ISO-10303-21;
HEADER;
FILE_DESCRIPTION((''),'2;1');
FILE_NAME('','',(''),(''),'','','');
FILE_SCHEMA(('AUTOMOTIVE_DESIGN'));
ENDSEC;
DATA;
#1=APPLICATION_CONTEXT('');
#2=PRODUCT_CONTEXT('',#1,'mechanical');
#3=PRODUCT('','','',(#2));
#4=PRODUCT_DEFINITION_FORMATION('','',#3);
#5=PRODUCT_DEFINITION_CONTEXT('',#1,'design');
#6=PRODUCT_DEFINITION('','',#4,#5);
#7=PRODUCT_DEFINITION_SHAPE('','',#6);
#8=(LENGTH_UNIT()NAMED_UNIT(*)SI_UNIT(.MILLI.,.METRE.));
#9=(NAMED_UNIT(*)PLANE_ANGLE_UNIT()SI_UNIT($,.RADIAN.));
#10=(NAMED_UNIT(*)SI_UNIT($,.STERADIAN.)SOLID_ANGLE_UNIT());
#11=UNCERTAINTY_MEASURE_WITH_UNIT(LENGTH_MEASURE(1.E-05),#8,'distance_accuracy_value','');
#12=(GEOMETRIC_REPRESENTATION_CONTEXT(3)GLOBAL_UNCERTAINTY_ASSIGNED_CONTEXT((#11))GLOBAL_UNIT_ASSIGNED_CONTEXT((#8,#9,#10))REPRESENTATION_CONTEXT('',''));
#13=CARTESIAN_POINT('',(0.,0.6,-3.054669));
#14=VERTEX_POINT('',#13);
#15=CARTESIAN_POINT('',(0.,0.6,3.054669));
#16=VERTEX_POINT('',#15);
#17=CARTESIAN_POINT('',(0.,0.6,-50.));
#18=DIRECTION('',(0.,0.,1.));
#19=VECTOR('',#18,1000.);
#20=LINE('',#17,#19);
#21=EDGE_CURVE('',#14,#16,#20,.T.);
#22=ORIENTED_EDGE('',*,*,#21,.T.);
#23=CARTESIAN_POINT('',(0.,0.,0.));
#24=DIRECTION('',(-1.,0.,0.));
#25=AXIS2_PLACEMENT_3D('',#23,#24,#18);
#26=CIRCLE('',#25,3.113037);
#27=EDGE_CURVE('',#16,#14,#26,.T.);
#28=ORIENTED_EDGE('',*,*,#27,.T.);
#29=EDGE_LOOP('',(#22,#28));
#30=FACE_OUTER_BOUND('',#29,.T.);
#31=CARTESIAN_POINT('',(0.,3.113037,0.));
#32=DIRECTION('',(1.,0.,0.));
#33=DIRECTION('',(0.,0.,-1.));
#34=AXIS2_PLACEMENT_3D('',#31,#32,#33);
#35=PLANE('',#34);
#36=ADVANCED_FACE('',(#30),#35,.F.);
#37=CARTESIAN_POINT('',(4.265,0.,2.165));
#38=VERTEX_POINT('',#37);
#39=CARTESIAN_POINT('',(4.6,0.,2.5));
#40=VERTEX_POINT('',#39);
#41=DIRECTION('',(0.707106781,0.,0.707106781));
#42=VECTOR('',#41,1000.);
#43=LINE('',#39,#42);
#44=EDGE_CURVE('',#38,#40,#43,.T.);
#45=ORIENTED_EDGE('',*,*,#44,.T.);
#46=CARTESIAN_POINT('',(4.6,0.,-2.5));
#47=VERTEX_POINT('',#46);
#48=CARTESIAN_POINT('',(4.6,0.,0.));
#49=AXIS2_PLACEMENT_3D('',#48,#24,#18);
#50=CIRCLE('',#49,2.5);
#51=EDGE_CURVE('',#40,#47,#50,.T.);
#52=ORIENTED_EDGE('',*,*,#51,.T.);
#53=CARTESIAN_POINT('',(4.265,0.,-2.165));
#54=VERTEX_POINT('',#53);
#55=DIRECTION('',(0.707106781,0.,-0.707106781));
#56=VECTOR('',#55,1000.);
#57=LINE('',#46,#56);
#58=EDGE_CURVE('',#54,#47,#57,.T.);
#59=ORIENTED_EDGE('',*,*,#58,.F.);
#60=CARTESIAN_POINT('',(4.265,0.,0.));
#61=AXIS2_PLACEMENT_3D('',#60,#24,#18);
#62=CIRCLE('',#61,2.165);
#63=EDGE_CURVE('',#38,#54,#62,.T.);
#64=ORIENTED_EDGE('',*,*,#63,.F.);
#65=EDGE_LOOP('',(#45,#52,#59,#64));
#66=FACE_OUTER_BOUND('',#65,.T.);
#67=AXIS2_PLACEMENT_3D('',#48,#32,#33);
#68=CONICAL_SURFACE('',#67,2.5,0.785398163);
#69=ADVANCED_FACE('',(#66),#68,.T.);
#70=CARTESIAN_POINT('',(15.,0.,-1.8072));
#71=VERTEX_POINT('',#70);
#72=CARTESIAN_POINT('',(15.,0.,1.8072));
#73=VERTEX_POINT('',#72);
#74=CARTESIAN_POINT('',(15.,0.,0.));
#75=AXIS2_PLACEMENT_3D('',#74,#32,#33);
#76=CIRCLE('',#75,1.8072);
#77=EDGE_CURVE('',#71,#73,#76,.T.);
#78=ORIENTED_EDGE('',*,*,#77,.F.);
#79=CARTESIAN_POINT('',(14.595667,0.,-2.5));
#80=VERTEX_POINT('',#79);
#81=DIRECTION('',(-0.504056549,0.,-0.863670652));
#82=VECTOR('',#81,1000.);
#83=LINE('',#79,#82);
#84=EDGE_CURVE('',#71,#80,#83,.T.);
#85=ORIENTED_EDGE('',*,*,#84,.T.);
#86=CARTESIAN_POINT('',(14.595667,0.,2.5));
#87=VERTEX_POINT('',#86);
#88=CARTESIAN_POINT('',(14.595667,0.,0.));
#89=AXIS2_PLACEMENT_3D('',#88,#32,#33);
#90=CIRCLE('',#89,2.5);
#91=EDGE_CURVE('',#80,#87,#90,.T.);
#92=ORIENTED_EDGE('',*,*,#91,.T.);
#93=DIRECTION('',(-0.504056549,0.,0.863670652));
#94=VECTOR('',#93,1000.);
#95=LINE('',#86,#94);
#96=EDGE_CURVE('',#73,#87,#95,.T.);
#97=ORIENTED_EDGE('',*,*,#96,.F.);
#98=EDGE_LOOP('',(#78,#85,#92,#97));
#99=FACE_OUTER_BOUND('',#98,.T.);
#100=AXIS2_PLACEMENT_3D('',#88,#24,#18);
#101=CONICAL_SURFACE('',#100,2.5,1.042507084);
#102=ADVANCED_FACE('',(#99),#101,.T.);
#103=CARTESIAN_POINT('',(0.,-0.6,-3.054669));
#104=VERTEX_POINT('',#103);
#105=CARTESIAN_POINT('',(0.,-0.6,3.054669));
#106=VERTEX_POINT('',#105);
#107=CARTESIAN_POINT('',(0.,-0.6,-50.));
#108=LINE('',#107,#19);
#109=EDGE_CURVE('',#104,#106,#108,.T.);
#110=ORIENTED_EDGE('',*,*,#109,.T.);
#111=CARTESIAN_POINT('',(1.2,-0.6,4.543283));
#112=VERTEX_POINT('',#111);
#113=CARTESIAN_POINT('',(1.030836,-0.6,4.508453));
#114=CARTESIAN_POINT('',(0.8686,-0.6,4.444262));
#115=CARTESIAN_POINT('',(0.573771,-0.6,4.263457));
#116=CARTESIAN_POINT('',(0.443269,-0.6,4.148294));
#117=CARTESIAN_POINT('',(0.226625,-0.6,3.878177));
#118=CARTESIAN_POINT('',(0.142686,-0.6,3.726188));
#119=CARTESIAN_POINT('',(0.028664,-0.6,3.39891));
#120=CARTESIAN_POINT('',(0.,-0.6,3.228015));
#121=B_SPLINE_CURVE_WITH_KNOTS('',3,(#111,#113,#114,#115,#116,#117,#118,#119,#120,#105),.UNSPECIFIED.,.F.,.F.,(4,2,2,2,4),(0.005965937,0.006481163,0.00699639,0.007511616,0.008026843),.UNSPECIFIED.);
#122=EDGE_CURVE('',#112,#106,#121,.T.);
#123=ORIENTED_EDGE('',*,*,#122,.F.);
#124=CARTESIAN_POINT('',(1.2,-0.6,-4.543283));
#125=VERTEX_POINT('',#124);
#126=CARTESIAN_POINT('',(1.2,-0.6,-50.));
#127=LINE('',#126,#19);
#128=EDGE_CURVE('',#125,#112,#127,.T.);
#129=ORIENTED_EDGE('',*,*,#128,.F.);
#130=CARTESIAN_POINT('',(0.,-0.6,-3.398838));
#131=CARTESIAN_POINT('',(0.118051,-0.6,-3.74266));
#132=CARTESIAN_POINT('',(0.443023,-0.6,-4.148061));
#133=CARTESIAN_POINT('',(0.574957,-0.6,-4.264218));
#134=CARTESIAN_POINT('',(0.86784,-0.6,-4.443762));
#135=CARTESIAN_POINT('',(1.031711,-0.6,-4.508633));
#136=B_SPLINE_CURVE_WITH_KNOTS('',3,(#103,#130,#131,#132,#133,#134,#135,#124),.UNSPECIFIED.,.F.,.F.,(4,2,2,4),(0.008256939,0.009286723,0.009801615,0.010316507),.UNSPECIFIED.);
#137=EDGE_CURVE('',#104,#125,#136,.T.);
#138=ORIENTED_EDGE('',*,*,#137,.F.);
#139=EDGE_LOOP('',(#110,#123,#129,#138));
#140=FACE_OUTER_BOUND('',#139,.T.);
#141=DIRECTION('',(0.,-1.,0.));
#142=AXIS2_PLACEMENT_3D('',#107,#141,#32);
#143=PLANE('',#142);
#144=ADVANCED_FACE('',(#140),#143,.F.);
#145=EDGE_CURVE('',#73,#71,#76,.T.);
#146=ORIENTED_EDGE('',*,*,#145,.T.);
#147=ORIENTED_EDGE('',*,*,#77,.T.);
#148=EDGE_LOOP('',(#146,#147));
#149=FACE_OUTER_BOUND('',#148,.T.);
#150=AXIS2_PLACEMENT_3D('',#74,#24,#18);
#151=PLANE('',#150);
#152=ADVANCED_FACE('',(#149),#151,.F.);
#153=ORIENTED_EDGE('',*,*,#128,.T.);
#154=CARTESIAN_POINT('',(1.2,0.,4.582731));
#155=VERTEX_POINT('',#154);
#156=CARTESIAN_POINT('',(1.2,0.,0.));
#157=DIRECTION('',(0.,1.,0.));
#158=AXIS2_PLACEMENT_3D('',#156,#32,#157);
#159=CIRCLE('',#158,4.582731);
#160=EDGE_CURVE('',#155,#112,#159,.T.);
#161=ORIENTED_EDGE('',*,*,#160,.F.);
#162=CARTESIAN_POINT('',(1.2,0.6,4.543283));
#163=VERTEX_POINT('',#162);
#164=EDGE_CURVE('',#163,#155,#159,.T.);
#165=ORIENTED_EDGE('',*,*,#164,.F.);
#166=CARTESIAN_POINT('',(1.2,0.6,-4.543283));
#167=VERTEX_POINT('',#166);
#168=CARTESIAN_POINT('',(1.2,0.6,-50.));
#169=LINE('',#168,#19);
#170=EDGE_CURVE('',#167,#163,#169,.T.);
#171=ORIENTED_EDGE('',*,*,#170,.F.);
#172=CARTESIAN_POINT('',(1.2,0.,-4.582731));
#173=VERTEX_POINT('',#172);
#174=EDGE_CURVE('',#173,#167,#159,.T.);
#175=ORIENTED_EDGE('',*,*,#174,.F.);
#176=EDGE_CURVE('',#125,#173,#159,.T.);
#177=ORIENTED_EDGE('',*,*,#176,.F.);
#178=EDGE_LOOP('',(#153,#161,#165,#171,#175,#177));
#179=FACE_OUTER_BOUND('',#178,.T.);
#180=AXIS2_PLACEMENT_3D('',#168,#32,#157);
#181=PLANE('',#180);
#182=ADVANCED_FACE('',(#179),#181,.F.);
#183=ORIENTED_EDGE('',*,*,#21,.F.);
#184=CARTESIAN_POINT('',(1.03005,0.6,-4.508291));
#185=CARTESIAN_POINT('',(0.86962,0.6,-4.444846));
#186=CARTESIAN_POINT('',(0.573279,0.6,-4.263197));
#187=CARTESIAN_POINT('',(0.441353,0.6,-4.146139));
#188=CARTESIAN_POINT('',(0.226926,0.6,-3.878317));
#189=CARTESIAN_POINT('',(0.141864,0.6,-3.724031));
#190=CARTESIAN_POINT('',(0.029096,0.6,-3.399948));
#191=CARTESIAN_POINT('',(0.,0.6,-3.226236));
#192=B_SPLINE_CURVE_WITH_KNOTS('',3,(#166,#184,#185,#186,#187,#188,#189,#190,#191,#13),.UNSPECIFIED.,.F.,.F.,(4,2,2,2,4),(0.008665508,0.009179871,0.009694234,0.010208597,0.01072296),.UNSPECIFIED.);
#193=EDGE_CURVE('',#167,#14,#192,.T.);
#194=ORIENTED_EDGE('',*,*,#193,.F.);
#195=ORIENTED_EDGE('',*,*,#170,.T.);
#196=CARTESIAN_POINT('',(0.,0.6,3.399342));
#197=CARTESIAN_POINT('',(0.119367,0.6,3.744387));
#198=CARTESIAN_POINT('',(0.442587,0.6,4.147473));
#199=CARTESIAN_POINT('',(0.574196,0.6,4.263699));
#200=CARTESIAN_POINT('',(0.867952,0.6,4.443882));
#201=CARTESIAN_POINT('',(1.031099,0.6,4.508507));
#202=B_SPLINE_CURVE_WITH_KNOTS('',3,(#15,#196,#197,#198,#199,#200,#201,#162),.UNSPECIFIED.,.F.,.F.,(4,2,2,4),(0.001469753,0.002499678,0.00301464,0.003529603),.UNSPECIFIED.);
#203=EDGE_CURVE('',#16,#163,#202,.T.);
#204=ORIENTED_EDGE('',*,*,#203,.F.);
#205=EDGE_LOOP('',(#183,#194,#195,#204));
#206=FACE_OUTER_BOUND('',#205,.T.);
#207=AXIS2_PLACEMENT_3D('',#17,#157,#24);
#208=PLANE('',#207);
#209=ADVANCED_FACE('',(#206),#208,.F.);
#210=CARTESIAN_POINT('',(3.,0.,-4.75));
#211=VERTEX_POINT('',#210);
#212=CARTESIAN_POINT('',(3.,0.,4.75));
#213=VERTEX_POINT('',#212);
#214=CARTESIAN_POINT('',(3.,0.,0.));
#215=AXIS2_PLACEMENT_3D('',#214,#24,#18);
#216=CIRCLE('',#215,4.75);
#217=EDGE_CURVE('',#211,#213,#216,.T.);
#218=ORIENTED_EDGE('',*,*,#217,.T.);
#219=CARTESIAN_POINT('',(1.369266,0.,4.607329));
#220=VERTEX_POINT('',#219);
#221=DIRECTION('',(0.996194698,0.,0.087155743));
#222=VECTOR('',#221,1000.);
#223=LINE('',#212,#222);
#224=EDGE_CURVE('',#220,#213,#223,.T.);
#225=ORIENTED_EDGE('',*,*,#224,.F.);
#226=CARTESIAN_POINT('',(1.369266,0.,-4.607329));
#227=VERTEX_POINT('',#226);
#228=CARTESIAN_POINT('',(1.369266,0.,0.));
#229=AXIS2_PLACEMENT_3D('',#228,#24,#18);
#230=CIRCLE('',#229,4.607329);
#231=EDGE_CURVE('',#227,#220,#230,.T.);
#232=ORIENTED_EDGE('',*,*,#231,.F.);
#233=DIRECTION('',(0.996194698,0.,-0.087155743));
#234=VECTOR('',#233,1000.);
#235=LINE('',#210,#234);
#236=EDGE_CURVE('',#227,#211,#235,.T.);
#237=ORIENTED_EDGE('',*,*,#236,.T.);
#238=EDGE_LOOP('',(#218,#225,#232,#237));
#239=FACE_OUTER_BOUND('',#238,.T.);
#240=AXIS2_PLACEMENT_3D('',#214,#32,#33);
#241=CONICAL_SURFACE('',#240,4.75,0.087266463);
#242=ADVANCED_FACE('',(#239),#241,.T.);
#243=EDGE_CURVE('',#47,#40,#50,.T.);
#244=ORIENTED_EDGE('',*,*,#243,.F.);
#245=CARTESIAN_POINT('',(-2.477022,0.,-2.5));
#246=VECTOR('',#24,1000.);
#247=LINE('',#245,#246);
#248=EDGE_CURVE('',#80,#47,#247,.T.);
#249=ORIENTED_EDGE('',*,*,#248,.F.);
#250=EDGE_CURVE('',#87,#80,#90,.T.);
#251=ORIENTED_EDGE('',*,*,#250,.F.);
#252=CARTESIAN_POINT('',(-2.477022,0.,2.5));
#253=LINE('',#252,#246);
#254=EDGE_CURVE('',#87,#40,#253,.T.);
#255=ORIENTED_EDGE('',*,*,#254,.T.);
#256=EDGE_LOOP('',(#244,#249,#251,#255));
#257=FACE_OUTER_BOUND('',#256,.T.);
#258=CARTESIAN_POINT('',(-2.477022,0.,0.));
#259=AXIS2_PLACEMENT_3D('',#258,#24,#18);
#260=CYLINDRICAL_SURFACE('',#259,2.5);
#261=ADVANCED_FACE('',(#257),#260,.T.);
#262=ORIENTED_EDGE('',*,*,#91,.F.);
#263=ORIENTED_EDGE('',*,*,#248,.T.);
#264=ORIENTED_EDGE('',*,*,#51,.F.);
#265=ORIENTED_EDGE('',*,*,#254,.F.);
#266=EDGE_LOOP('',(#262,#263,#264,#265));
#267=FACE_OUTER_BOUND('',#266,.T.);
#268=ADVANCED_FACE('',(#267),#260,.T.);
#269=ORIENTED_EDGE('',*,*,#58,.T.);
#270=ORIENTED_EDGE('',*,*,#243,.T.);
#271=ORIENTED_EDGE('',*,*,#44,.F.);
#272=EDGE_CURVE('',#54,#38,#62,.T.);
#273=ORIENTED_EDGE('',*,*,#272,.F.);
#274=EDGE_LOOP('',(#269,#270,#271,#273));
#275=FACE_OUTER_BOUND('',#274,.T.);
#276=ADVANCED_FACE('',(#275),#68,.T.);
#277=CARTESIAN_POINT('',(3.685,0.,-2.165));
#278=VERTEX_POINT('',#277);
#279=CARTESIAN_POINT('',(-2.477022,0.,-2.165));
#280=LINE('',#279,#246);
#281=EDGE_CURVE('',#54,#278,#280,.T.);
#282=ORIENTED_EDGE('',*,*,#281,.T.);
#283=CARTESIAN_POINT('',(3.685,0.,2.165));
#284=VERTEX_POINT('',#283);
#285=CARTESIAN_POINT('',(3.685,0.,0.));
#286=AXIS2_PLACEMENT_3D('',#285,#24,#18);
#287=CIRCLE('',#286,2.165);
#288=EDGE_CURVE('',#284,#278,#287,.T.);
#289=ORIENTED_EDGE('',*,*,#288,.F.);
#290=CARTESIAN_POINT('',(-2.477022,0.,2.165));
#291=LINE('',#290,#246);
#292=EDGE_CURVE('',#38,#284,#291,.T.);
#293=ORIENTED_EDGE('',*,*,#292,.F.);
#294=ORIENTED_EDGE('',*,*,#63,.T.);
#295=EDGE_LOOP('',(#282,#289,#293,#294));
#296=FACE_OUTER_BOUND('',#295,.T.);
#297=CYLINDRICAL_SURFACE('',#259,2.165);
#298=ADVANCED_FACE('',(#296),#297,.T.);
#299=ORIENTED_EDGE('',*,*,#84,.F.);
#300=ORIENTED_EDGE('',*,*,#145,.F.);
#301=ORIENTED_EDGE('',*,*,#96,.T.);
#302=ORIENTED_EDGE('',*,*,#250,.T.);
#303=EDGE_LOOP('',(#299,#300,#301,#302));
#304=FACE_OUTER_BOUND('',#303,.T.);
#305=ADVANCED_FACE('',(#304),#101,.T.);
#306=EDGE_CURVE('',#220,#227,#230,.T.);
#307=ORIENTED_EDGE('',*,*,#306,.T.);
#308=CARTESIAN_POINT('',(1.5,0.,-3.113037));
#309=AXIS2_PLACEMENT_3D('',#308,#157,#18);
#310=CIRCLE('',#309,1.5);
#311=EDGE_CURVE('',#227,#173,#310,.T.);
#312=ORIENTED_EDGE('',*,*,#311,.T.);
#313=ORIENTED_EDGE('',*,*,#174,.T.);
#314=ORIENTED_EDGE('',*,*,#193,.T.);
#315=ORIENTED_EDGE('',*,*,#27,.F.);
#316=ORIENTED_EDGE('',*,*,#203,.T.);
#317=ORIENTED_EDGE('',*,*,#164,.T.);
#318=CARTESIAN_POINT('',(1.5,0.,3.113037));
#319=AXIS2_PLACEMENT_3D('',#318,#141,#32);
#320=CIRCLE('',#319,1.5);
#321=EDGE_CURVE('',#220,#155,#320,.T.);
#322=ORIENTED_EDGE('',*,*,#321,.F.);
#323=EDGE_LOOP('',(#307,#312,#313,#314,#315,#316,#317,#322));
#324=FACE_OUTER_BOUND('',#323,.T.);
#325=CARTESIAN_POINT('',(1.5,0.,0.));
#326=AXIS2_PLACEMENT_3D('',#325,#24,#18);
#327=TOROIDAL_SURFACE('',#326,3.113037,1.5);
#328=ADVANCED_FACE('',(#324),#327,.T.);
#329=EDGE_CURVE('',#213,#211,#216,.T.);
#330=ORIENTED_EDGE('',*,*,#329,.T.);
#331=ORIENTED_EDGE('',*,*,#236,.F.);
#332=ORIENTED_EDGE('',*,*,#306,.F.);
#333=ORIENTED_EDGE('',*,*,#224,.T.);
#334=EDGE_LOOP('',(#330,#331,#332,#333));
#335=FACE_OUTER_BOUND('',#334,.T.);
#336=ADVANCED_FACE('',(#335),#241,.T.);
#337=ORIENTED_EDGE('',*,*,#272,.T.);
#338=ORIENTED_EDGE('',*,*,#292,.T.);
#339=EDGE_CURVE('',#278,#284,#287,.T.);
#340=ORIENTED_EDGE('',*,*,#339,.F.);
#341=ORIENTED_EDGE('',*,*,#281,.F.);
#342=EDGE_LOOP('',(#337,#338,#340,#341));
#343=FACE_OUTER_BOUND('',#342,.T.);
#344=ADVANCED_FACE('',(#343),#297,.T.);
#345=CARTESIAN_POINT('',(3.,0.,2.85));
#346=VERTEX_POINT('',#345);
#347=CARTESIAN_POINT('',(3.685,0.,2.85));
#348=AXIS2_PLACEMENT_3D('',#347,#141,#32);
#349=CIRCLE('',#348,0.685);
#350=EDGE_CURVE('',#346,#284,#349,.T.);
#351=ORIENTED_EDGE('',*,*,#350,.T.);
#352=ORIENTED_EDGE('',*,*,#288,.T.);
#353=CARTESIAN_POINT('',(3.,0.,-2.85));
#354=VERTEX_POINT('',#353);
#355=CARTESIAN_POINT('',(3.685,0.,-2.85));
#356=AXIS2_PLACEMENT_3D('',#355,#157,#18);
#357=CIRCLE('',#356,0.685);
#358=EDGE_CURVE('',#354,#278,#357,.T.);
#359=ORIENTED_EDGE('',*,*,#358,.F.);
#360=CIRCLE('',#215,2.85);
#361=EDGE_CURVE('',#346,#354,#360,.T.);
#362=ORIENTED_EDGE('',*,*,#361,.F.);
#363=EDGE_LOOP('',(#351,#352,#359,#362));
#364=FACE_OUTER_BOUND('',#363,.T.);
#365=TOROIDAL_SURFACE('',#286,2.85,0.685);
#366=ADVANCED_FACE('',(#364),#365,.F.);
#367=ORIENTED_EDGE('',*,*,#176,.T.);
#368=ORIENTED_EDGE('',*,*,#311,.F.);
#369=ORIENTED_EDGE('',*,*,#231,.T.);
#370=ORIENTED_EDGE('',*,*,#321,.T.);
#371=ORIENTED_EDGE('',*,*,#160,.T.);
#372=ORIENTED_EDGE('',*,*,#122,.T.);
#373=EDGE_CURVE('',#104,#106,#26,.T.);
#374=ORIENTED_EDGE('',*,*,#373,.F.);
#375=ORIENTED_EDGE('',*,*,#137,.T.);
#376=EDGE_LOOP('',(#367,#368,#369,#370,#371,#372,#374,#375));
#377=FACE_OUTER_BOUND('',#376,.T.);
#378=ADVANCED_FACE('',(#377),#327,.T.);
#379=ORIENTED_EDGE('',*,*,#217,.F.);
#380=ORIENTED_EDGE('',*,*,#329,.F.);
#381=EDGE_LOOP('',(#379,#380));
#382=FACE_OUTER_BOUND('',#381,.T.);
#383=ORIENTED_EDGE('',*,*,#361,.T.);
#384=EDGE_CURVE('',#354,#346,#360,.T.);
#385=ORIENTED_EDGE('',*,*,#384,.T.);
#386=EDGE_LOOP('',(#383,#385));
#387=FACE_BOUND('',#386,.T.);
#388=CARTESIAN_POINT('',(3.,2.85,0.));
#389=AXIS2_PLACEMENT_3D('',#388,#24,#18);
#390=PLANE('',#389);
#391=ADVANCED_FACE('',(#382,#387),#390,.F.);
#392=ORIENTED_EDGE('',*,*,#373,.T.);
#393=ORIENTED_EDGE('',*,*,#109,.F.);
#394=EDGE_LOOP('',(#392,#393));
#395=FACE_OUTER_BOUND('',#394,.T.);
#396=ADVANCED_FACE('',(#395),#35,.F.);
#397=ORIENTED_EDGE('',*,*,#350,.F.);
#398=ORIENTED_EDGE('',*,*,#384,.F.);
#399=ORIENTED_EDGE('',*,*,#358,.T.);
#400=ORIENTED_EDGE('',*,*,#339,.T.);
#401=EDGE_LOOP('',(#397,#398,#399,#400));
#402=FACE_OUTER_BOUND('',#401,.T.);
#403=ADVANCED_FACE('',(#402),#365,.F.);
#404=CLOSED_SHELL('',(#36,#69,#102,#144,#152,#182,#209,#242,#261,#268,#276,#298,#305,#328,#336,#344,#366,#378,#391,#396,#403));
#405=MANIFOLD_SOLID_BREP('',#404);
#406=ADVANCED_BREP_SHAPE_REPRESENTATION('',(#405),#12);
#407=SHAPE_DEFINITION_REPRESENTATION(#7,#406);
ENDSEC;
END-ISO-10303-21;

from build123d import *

# Parameters (mm, degrees)
SKETCH4_W          = 1.2
SKETCH4_H          = 1.2
CUT_EXTRUDE1_DEPTH = 50


with BuildPart() as part:
    # Sketch3 → Boss-Revolve (revolve)
    with BuildSketch(Plane.XY, mode=Mode.PRIVATE) as boss_revolve_sk:
        with BuildLine():
            Line((0, 0), (15, 0))
            Line((15, 0), (15, 2.5))
            Line((15, 2.5), (4.6, 2.5))
            Line((4.6, 2.5), (4.265, 2.165))
            Line((4.265, 2.165), (3.685, 2.165))
            ThreePointArc((3.685, 2.165), (3.200631855, 2.365631855), (3, 2.85))
            Line((3, 2.85), (3, 4.75))
            Line((3, 4.75), (1.369266386, 4.607329296))
            ThreePointArc((1.369266386, 4.607329296), (0.394083995, 4.12642256), (0, 3.113037248))
            Line((0, 3.113037248), (0, 0))
        make_face()
    revolve(boss_revolve_sk.sketch.rotate(Axis((-2.477021524, 0, 0), (1, 0, 0)), 90), axis=Axis((-2.477021524, 0, 0), (1, 0, 0)))

    # Sketch4 → Cut-Extrude1 (cut, symmetric)
    with BuildSketch(Plane.XY):
        with Locations((0.6, 0)):
            Rectangle(SKETCH4_W, SKETCH4_H)
    extrude(amount=CUT_EXTRUDE1_DEPTH, both=True, mode=Mode.SUBTRACT)

    # Sketch5 → Cut-Revolve1 (revolve, cut)
    with BuildSketch(Plane.XY, mode=Mode.PRIVATE) as cut_revolve1_sk:
        Polygon((14.595667195, 2.5), (15.395667195, 2.5), (15, 1.8072), align=None)
    revolve(cut_revolve1_sk.sketch.rotate(Axis((6.174994867, 0, 0), (-1, 0, 0)), 270), axis=Axis((6.174994867, 0, 0), (-1, 0, 0)), mode=Mode.SUBTRACT)


solid = part.part
